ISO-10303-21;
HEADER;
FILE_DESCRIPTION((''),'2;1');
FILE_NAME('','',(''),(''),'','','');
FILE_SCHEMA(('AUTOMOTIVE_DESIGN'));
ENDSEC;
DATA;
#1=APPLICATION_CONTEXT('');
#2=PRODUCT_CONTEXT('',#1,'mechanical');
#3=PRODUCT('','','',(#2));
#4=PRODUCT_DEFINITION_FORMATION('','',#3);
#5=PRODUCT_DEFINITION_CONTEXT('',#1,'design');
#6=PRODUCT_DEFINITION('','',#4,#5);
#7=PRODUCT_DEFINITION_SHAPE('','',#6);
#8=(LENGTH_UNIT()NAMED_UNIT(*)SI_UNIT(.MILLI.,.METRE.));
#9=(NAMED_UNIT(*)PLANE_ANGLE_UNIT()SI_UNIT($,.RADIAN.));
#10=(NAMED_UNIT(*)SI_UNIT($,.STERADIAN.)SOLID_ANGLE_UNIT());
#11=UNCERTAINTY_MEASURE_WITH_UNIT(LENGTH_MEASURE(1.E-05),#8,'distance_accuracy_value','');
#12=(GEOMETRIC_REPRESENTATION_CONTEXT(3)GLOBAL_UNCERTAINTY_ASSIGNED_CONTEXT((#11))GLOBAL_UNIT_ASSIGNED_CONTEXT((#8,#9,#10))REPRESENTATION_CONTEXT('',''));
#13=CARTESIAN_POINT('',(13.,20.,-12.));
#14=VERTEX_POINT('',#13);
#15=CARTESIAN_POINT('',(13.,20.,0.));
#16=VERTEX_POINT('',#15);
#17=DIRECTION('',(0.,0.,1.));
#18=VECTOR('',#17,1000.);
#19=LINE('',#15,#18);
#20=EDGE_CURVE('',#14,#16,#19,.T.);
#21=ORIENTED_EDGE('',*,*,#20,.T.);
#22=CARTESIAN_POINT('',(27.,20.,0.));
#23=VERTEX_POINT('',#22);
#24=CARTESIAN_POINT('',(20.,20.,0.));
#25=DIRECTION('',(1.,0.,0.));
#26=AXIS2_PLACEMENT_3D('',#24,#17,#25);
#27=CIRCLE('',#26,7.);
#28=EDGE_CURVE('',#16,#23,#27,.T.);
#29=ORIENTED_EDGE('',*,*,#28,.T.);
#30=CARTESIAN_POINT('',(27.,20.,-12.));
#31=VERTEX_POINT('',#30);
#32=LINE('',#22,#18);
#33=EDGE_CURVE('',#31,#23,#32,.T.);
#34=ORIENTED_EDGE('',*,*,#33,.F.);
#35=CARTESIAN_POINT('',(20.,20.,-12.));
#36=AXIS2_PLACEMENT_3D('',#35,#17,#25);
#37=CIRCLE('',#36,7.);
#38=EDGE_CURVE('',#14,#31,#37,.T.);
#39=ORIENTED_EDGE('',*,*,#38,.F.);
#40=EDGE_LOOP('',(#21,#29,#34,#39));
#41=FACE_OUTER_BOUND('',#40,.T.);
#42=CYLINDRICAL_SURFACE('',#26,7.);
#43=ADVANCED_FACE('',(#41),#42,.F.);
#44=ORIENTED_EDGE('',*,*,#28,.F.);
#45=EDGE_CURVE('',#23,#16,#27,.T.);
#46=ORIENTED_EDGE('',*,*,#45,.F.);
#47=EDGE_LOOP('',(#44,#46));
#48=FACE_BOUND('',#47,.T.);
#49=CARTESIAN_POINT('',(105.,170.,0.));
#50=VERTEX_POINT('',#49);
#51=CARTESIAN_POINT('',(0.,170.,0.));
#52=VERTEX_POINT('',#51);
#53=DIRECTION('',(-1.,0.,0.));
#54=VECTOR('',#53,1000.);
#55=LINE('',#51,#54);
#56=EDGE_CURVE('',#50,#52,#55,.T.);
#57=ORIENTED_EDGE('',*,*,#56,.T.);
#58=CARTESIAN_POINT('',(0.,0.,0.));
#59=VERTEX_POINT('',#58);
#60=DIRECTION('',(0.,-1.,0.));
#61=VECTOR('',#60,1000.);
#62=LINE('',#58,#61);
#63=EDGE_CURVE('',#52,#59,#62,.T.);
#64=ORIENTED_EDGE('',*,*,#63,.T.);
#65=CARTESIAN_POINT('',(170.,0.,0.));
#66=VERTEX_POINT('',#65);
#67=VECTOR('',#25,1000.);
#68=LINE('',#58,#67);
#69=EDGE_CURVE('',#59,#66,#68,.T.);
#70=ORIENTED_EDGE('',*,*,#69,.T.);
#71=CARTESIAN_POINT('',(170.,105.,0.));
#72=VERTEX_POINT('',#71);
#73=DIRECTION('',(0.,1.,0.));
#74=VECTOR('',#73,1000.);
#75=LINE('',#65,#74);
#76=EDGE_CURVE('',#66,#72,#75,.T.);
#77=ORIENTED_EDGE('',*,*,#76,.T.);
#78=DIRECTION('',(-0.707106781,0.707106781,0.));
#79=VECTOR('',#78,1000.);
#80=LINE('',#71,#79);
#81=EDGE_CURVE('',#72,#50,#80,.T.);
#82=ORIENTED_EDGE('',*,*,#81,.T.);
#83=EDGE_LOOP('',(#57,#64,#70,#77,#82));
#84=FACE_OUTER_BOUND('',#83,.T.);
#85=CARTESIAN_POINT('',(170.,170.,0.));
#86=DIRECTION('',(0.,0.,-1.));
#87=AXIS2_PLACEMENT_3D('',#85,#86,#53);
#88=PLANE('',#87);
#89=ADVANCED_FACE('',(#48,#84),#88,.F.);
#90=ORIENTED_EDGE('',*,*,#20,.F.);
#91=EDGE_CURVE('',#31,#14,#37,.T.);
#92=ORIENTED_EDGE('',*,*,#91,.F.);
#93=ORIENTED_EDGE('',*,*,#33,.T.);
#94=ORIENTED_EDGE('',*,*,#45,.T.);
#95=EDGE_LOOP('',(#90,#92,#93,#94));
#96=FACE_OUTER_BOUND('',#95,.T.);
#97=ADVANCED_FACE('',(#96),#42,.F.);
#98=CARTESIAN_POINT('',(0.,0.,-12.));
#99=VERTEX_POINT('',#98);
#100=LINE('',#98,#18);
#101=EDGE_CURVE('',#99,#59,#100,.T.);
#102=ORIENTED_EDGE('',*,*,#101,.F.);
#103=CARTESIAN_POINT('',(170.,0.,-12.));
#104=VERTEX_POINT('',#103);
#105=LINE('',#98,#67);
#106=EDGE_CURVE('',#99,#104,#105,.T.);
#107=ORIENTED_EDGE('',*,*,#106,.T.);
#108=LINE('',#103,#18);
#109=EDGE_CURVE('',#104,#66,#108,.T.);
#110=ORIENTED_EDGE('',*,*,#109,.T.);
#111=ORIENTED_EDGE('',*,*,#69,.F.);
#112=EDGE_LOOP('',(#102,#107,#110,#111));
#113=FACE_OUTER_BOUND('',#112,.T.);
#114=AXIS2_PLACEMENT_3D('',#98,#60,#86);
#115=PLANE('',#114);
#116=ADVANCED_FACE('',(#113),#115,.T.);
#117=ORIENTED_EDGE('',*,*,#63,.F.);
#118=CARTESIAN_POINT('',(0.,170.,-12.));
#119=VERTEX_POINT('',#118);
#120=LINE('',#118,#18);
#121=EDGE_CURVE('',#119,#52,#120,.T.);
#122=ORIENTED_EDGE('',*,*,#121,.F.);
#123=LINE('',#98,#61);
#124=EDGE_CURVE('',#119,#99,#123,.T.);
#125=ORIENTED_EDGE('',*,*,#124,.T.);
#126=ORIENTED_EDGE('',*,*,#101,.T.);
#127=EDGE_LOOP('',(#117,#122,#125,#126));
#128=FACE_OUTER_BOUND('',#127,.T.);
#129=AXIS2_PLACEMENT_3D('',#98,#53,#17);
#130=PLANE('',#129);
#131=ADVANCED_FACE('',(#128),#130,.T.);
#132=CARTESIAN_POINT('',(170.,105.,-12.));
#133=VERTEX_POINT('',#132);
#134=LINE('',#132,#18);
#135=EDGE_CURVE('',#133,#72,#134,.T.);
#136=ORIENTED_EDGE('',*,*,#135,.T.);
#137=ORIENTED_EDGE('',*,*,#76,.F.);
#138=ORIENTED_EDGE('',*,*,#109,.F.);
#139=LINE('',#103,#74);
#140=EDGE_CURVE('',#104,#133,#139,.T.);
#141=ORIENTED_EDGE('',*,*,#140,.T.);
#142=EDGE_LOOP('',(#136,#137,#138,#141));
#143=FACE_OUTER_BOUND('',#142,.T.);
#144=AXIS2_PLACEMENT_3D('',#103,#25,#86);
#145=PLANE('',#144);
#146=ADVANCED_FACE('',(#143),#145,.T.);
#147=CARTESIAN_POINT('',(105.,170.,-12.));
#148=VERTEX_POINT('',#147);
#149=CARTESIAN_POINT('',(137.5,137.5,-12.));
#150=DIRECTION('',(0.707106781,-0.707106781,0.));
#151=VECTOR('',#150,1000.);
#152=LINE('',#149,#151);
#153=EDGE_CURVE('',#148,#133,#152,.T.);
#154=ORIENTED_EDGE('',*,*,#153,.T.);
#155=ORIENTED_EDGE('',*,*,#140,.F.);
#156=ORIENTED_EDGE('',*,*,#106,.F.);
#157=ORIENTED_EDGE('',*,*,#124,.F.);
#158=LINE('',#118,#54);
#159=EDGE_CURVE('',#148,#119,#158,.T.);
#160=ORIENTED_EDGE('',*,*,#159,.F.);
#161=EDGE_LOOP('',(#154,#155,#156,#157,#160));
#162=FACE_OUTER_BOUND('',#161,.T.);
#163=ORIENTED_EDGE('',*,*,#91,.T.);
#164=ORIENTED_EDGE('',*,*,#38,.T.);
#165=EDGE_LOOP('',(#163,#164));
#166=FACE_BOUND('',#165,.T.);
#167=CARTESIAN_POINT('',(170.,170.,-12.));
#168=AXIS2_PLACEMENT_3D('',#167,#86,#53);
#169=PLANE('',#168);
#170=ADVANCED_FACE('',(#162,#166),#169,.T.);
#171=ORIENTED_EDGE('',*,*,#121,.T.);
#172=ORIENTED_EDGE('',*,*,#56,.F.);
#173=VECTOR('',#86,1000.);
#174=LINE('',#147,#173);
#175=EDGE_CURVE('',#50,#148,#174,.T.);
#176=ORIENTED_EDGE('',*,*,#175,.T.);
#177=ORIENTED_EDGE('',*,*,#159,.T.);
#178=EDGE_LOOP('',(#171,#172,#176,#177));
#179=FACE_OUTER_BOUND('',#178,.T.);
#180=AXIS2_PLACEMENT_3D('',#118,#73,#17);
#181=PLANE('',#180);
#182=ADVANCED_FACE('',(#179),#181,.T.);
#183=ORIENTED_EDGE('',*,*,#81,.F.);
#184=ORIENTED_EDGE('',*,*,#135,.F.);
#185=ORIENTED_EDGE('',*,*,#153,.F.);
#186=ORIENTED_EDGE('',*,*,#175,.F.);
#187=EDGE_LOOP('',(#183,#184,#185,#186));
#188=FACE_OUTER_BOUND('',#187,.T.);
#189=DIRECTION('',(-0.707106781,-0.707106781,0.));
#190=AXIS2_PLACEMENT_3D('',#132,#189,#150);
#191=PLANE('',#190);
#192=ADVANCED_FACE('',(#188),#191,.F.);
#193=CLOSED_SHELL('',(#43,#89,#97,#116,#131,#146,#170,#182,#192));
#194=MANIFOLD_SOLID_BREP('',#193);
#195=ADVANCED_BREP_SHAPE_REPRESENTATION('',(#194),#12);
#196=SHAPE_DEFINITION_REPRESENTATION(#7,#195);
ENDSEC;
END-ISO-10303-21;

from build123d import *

# Parameters (mm, degrees)
SKETCH1_W              = 170
SKETCH1_H              = 170
EXTRUDE1_DEPTH         = 12
M16X2_0_TAPPED_HOLE1_D = 14
CHAMFER1_SIZE          = 65


with BuildPart() as part:
    # Sketch1 → Extrude1 (new body)
    with BuildSketch(Plane.XY):
        with Locations((85, 85)):
            Rectangle(SKETCH1_W, SKETCH1_H)
    extrude(amount=-EXTRUDE1_DEPTH)

    # M16x2.0 Tapped Hole1 (through all)
    with Locations(Plane.XY):
        with Locations((20, 20)):
            Hole(M16X2_0_TAPPED_HOLE1_D / 2)

    # Chamfer1
    chamfer1_edges = [part.edges().sort_by_distance(p)[0] for p in [
        (170, 170, -6),
    ]]
    chamfer(chamfer1_edges, length=CHAMFER1_SIZE)


solid = part.part
